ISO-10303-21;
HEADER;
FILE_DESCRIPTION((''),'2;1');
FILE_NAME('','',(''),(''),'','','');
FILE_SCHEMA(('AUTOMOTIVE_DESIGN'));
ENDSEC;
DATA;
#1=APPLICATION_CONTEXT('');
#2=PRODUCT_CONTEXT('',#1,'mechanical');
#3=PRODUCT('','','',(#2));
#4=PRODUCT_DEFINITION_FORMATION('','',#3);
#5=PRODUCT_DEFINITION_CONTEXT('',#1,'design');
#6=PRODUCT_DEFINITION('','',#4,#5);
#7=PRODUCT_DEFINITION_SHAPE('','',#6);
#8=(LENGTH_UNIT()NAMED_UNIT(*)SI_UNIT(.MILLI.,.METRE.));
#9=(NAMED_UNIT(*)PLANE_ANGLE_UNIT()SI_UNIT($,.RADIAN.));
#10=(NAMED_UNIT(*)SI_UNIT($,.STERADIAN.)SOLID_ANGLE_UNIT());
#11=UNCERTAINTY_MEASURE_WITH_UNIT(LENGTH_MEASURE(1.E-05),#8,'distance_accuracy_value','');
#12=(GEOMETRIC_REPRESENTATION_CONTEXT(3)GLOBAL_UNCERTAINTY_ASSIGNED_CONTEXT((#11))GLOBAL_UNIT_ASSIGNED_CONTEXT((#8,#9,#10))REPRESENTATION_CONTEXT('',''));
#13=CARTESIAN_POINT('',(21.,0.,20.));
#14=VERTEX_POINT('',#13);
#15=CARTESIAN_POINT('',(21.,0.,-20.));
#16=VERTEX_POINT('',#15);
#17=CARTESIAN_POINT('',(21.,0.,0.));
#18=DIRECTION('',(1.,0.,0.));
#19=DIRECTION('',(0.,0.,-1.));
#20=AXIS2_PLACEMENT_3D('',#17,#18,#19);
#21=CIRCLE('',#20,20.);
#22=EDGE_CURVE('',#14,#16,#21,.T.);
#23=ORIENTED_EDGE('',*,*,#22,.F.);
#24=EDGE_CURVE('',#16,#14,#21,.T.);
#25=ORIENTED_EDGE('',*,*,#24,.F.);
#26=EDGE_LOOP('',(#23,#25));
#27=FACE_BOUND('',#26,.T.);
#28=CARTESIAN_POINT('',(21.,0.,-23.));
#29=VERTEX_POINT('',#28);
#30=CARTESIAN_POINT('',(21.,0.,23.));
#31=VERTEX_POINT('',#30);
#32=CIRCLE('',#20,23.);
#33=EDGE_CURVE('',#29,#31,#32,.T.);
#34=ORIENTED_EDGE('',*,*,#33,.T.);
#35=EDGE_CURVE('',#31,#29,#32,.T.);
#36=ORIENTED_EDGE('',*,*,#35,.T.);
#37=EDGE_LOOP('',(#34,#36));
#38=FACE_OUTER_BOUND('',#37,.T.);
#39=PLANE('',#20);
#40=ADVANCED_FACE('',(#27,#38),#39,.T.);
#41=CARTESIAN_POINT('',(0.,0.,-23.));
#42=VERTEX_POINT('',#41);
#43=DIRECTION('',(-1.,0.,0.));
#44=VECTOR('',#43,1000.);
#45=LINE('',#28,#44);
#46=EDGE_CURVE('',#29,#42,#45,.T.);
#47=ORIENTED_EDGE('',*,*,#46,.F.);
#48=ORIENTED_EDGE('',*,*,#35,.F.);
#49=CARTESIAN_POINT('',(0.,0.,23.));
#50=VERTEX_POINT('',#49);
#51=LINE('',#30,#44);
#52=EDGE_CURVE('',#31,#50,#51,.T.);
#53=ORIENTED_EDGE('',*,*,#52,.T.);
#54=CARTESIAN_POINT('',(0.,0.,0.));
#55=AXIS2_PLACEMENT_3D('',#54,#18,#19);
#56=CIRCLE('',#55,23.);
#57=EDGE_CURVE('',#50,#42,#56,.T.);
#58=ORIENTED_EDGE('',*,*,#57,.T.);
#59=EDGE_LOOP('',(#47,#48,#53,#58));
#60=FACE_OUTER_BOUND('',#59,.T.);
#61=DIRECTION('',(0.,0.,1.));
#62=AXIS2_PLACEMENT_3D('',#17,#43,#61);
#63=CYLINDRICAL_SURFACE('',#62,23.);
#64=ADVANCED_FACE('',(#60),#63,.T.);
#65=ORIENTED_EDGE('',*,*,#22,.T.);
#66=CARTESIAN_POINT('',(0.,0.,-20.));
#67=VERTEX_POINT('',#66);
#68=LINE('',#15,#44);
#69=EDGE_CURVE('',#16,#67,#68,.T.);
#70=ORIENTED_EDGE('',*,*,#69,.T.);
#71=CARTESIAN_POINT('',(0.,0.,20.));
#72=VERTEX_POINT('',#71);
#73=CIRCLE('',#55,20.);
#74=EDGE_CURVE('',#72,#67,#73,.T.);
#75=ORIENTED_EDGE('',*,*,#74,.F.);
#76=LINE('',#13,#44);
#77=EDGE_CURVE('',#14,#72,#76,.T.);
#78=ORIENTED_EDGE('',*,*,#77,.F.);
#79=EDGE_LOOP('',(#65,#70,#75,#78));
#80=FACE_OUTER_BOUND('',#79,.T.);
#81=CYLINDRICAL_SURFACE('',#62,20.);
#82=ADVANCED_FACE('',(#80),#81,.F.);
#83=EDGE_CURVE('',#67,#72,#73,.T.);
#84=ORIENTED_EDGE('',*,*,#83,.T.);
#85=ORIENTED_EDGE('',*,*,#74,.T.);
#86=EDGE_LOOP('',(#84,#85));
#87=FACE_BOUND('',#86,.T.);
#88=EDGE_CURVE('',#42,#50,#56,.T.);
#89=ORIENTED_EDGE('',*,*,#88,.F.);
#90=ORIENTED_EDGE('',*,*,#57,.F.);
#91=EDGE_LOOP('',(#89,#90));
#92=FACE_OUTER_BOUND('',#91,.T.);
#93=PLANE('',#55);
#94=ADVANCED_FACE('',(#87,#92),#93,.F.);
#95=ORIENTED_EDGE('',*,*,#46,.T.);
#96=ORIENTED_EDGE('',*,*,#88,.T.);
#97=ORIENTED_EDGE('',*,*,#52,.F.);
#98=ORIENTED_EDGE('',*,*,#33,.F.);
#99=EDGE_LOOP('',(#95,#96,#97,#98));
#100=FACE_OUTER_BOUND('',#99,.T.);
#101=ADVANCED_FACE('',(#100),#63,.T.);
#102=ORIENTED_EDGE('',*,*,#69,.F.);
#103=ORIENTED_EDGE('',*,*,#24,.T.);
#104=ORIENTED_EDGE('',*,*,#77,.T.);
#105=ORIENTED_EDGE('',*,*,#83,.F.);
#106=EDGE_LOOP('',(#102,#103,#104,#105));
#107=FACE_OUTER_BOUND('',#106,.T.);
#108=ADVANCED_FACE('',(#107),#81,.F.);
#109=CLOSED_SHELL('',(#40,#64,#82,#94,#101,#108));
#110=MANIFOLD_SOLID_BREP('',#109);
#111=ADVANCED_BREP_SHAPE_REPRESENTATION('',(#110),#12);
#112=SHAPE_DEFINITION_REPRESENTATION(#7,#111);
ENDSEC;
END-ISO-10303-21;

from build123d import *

# Parameters (mm, degrees)
SKETCH_1_R      = 23
SKETCH_1_R_2    = 20
EXTRUDE_1_DEPTH = 21


with BuildPart() as part:
    # 草图1 → 凸台-拉伸1 (new body)
    with BuildSketch(Plane(origin=(0, 0, 0), x_dir=(0, 0, -1), z_dir=(1, 0, 0))):
        with Locations(Location((0, 0, 0), (0, 0, 180))):
            Circle(SKETCH_1_R)
        with Locations(Location((0, 0, 0), (0, 0, 180))):
            Circle(SKETCH_1_R_2, mode=Mode.SUBTRACT)
    extrude(amount=EXTRUDE_1_DEPTH)


solid = part.part
